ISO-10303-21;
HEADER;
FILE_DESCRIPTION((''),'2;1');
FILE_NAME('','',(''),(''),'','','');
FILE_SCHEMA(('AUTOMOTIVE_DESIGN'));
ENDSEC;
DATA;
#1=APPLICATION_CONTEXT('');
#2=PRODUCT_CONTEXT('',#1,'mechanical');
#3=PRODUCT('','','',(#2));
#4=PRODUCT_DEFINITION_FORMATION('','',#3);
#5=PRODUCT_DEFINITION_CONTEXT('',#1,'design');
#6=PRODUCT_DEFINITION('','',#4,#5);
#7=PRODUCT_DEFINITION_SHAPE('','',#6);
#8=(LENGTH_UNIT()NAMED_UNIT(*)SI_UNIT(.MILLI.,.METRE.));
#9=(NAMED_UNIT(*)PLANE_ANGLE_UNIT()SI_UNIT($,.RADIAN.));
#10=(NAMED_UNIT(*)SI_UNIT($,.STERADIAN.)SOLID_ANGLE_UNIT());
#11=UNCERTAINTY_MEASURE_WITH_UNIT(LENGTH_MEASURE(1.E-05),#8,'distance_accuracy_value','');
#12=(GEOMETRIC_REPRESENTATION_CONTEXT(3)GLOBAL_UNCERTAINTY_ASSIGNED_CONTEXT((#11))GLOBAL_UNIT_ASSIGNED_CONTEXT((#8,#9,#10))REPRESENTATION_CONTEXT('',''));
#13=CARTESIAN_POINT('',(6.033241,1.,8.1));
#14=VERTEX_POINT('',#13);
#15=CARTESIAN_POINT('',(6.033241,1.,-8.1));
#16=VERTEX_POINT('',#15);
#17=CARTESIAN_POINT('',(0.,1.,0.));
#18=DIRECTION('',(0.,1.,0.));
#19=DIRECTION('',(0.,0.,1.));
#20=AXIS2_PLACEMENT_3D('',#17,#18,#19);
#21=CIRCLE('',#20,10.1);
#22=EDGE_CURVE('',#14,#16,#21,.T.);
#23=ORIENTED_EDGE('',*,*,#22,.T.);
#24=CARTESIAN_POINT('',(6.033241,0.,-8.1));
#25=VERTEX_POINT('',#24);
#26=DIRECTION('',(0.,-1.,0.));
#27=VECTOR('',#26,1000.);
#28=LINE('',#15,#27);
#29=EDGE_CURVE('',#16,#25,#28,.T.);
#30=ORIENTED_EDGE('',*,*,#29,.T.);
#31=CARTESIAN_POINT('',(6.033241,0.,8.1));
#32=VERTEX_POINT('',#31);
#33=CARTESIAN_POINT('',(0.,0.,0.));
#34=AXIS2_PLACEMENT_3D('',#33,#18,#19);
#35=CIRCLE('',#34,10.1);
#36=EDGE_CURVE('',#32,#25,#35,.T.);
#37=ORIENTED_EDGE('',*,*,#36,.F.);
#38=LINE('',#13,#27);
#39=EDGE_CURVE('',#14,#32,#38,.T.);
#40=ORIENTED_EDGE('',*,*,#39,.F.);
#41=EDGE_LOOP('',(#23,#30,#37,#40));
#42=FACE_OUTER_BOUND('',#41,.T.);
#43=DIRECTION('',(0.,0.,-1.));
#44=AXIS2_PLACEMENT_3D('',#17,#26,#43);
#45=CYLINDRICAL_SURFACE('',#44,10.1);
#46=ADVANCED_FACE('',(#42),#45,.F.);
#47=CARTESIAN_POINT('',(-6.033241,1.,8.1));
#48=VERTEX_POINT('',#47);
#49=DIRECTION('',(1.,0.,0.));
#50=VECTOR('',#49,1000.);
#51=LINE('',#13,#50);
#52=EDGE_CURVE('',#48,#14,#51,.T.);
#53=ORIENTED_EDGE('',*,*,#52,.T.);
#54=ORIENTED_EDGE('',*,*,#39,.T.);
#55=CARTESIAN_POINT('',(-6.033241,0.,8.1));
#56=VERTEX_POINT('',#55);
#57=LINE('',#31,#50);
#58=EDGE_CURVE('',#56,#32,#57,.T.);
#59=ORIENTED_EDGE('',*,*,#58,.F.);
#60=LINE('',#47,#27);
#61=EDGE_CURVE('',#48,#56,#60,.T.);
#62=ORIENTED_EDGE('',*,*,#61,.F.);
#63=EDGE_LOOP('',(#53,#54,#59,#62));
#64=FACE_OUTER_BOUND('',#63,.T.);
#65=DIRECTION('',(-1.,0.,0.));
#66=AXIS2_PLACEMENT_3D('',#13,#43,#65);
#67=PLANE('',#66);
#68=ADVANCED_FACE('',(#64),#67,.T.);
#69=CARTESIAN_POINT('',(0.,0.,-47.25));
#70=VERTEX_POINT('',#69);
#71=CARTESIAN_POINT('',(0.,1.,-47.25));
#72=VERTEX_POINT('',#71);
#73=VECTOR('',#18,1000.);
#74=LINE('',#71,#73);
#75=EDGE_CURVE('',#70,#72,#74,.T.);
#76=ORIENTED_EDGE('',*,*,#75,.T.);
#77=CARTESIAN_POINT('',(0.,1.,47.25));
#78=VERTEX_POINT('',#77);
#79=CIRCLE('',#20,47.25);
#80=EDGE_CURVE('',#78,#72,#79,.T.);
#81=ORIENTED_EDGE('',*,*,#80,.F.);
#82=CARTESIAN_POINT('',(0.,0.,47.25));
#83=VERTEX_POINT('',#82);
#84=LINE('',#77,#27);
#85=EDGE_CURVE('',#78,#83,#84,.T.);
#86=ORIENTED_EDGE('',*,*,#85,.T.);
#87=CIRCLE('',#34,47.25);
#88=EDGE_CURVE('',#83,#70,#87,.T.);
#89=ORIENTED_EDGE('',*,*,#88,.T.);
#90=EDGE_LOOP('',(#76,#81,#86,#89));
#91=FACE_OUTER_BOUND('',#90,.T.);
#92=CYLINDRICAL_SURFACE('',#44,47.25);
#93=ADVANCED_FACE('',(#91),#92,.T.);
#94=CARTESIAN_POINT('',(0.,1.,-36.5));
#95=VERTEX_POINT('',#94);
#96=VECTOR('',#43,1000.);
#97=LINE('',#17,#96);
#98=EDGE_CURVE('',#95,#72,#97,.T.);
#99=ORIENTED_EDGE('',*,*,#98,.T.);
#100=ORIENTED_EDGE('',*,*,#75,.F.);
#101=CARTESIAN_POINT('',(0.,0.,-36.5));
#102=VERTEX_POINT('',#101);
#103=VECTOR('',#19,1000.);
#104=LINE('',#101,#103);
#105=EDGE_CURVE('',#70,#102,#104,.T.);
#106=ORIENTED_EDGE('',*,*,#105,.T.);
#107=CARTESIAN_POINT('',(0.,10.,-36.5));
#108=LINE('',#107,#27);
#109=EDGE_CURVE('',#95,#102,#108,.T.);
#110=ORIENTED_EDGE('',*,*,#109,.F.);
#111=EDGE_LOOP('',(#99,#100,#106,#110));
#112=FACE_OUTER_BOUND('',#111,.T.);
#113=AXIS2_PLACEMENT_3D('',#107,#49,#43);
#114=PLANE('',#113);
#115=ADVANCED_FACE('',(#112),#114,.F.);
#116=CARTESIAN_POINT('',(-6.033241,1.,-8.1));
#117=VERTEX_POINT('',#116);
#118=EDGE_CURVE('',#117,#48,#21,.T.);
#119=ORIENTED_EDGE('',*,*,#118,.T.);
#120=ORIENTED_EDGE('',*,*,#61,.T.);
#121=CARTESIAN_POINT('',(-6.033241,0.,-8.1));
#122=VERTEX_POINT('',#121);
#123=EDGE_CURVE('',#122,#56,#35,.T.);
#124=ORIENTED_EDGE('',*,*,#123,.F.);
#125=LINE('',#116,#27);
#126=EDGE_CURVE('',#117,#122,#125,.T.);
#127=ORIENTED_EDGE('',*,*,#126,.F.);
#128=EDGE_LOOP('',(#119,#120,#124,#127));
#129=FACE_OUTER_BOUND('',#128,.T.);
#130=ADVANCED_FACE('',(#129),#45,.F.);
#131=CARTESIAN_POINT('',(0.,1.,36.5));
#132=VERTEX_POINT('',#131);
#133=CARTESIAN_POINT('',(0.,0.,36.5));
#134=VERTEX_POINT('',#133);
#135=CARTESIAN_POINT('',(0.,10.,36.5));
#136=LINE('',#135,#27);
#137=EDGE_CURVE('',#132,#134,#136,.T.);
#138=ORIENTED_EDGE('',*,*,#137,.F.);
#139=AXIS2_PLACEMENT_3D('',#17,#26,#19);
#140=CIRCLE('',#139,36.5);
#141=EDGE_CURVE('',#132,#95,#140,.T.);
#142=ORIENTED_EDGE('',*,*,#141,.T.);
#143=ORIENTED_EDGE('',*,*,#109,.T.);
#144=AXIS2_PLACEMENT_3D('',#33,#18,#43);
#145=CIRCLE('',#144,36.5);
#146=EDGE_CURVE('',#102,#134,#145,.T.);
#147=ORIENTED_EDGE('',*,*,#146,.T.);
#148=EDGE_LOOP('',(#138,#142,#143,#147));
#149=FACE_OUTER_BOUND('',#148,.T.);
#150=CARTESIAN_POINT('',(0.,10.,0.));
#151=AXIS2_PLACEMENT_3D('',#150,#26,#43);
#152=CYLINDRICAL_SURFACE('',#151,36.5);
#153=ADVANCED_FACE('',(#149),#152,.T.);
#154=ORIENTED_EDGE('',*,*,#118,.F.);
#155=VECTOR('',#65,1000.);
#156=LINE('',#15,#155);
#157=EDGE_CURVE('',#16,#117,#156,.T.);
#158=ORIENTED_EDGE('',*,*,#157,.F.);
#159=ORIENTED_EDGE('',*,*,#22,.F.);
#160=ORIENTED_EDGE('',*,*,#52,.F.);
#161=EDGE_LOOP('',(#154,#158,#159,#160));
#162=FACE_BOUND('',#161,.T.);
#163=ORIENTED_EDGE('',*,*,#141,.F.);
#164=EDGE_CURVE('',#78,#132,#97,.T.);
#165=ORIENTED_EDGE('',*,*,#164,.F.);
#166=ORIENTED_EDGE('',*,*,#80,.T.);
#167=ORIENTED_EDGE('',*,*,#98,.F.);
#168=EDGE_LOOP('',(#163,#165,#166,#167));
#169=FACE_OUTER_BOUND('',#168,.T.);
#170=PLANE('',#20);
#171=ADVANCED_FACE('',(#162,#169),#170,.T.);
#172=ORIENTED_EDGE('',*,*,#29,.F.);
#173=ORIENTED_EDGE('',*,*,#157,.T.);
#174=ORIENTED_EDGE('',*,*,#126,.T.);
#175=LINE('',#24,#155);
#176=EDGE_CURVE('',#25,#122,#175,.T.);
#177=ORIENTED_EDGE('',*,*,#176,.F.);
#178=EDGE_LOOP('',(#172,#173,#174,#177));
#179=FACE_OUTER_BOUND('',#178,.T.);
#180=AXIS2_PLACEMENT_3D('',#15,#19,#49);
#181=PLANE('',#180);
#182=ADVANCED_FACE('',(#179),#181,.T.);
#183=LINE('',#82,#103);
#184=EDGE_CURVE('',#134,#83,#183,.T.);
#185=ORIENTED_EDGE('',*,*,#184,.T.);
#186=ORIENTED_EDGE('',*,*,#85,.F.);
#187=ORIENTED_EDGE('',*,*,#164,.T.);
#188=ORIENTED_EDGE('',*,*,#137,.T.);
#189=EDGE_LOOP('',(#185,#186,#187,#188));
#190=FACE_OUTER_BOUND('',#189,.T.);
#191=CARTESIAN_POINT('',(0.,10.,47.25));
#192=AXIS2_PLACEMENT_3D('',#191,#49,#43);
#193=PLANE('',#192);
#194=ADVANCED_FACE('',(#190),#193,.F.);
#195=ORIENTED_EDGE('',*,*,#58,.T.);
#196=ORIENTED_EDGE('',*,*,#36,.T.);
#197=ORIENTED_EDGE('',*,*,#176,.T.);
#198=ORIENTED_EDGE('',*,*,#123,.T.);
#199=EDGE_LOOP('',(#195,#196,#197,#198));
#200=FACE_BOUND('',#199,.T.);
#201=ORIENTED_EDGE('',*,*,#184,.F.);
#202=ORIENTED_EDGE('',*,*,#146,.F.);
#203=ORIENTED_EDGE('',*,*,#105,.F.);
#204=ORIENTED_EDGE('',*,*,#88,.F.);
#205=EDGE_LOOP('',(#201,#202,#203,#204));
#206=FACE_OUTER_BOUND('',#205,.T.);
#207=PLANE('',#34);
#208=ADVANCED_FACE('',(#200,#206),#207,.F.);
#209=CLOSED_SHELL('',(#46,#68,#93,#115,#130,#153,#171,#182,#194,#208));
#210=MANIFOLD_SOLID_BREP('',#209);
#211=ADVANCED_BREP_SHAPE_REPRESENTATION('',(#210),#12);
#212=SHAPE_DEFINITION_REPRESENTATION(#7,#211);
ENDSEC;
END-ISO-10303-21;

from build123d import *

# Parameters (mm, degrees)
SKETCH1_R           = 47.25
SKETCH1_R_2         = 10.1
BOSS_EXTRUDE1_DEPTH = 1
BOSS_EXTRUDE2_DEPTH = 1
CUT_EXTRUDE1_DEPTH  = 10


with BuildPart() as part:
    # Sketch1 → Boss-Extrude1 (new body)
    with BuildSketch(Plane(origin=(0, 0, 0), x_dir=(1, 0, 0), z_dir=(0, 1, 0))):
        with Locations(Location((0, 0, 0), (0, 0, 270))):
            Circle(SKETCH1_R)
        with Locations(Location((0, 0, 0), (0, 0, 270))):
            Circle(SKETCH1_R_2, mode=Mode.SUBTRACT)
    extrude(amount=BOSS_EXTRUDE1_DEPTH)

    # Sketch2 → Boss-Extrude2 (add)
    with BuildSketch(Plane.XZ):
        with BuildLine():
            Line((6.033241252, -8.1), (-6.033241252, -8.1))
            ThreePointArc((-6.033241252, -8.1), (0, -10.1), (6.033241252, -8.1))
        make_face()
        with BuildLine():
            Line((6.033241252, 8.1), (-6.033241252, 8.1))
            ThreePointArc((-6.033241252, 8.1), (0, 10.1), (6.033241252, 8.1))
        make_face()
    extrude(amount=-BOSS_EXTRUDE2_DEPTH)

    # Sketch3 → Cut-Extrude1 (cut)
    with BuildSketch(Plane.XZ):
        with BuildLine():
            Line((0, 47.25), (0, 36.5))
            ThreePointArc((0, 36.5), (-36.5, 0), (0, -36.5))
            Line((0, -36.5), (0, -47.25))
            ThreePointArc((0, -47.25), (-47.25, 0), (0, 47.25))
        make_face()
    extrude(amount=-CUT_EXTRUDE1_DEPTH, mode=Mode.SUBTRACT)


solid = part.part
